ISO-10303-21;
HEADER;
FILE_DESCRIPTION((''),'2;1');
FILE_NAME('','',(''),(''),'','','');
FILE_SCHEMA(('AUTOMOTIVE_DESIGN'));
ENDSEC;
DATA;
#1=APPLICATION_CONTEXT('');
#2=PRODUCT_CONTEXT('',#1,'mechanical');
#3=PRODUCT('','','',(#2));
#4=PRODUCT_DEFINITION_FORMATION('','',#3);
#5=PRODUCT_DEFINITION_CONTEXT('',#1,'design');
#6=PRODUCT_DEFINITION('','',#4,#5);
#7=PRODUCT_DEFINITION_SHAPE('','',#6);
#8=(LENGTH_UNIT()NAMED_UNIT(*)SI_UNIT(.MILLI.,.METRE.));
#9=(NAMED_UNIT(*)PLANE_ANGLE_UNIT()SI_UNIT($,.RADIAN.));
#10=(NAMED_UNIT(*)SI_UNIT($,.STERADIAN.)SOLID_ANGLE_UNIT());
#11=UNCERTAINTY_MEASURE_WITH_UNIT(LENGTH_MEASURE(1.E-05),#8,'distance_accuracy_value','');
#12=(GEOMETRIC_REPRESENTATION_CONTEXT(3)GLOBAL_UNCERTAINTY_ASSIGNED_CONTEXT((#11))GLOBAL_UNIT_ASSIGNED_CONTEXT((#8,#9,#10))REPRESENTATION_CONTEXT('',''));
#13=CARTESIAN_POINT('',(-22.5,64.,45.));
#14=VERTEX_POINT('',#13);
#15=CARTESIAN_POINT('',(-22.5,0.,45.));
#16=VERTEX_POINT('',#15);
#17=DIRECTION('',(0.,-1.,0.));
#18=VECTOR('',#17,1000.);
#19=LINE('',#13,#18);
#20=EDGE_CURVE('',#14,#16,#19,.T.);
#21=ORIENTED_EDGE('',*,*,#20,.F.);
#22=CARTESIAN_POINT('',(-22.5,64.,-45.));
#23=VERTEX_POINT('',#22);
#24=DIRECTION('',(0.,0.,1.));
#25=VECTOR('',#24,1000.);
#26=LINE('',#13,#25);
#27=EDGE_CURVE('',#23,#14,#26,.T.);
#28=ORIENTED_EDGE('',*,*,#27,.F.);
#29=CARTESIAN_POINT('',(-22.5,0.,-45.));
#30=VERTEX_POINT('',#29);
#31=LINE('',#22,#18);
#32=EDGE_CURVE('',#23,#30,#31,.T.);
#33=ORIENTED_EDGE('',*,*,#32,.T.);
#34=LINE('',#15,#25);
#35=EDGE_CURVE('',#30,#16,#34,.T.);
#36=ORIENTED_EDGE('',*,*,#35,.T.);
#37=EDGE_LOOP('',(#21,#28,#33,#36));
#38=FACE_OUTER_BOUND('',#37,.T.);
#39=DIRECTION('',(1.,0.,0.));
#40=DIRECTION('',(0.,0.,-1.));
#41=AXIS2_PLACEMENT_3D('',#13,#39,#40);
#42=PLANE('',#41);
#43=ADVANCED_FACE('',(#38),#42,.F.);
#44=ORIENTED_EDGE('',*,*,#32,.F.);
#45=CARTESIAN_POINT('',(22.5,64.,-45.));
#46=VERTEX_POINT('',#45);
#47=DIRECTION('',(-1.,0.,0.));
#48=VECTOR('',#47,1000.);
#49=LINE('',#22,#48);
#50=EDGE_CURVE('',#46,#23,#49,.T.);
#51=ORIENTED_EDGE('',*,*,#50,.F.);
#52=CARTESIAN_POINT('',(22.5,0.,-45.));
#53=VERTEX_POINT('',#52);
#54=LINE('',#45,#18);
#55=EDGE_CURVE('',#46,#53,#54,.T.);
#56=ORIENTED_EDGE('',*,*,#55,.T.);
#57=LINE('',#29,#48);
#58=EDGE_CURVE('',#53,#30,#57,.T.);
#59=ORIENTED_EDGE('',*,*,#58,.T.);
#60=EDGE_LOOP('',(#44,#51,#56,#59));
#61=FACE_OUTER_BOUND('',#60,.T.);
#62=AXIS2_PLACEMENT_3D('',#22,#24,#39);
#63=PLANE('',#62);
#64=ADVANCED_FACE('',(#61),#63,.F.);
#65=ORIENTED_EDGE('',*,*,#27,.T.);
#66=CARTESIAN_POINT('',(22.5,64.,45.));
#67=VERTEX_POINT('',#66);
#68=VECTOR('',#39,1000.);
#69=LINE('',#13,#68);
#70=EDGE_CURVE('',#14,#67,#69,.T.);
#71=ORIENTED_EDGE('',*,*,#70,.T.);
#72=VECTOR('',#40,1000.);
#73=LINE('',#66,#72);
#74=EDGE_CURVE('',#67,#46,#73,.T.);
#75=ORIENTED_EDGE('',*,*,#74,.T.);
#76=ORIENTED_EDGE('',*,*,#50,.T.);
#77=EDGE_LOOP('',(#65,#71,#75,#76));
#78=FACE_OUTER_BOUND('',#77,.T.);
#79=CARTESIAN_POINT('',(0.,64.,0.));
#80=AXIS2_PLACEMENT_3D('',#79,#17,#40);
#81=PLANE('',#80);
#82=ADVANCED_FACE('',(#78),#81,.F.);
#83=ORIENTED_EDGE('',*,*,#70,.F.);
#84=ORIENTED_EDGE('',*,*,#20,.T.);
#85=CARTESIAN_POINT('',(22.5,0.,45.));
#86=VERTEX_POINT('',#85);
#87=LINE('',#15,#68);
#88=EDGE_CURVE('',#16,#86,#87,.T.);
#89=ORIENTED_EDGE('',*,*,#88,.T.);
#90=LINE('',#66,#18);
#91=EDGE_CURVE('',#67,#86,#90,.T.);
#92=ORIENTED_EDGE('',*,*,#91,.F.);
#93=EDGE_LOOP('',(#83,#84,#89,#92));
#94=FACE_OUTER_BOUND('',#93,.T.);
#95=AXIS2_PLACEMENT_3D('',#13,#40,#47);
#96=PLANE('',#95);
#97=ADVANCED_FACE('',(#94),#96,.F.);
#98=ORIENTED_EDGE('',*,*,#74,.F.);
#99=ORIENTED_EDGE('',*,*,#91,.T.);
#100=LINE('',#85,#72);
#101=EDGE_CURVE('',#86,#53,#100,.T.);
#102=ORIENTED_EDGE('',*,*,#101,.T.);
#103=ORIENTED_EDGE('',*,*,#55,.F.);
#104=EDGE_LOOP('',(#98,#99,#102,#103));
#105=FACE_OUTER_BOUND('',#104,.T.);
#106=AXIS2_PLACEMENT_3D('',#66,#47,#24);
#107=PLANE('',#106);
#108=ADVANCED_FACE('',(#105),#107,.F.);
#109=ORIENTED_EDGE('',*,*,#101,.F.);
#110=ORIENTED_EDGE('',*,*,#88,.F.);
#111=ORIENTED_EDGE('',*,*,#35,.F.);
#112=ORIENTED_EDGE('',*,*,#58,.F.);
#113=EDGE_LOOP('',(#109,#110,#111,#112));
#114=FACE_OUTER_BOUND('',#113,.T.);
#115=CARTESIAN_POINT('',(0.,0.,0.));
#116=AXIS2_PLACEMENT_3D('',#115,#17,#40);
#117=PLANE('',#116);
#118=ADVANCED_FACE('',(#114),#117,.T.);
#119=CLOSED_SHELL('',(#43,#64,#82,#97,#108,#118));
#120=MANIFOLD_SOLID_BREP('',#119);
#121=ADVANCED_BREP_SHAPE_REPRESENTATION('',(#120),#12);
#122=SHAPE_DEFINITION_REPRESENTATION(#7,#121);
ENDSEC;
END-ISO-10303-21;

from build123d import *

# Parameters (mm, degrees)
SKETCH_1_W      = 45
SKETCH_1_H      = 90
EXTRUDE_1_DEPTH = 64


with BuildPart() as part:
    # 草图1 → 凸台-拉伸1 (new body)
    with BuildSketch(Plane(origin=(0, 0, 0), x_dir=(1, 0, 0), z_dir=(0, 1, 0))):
        Rectangle(SKETCH_1_W, SKETCH_1_H)
    extrude(amount=EXTRUDE_1_DEPTH)


solid = part.part
